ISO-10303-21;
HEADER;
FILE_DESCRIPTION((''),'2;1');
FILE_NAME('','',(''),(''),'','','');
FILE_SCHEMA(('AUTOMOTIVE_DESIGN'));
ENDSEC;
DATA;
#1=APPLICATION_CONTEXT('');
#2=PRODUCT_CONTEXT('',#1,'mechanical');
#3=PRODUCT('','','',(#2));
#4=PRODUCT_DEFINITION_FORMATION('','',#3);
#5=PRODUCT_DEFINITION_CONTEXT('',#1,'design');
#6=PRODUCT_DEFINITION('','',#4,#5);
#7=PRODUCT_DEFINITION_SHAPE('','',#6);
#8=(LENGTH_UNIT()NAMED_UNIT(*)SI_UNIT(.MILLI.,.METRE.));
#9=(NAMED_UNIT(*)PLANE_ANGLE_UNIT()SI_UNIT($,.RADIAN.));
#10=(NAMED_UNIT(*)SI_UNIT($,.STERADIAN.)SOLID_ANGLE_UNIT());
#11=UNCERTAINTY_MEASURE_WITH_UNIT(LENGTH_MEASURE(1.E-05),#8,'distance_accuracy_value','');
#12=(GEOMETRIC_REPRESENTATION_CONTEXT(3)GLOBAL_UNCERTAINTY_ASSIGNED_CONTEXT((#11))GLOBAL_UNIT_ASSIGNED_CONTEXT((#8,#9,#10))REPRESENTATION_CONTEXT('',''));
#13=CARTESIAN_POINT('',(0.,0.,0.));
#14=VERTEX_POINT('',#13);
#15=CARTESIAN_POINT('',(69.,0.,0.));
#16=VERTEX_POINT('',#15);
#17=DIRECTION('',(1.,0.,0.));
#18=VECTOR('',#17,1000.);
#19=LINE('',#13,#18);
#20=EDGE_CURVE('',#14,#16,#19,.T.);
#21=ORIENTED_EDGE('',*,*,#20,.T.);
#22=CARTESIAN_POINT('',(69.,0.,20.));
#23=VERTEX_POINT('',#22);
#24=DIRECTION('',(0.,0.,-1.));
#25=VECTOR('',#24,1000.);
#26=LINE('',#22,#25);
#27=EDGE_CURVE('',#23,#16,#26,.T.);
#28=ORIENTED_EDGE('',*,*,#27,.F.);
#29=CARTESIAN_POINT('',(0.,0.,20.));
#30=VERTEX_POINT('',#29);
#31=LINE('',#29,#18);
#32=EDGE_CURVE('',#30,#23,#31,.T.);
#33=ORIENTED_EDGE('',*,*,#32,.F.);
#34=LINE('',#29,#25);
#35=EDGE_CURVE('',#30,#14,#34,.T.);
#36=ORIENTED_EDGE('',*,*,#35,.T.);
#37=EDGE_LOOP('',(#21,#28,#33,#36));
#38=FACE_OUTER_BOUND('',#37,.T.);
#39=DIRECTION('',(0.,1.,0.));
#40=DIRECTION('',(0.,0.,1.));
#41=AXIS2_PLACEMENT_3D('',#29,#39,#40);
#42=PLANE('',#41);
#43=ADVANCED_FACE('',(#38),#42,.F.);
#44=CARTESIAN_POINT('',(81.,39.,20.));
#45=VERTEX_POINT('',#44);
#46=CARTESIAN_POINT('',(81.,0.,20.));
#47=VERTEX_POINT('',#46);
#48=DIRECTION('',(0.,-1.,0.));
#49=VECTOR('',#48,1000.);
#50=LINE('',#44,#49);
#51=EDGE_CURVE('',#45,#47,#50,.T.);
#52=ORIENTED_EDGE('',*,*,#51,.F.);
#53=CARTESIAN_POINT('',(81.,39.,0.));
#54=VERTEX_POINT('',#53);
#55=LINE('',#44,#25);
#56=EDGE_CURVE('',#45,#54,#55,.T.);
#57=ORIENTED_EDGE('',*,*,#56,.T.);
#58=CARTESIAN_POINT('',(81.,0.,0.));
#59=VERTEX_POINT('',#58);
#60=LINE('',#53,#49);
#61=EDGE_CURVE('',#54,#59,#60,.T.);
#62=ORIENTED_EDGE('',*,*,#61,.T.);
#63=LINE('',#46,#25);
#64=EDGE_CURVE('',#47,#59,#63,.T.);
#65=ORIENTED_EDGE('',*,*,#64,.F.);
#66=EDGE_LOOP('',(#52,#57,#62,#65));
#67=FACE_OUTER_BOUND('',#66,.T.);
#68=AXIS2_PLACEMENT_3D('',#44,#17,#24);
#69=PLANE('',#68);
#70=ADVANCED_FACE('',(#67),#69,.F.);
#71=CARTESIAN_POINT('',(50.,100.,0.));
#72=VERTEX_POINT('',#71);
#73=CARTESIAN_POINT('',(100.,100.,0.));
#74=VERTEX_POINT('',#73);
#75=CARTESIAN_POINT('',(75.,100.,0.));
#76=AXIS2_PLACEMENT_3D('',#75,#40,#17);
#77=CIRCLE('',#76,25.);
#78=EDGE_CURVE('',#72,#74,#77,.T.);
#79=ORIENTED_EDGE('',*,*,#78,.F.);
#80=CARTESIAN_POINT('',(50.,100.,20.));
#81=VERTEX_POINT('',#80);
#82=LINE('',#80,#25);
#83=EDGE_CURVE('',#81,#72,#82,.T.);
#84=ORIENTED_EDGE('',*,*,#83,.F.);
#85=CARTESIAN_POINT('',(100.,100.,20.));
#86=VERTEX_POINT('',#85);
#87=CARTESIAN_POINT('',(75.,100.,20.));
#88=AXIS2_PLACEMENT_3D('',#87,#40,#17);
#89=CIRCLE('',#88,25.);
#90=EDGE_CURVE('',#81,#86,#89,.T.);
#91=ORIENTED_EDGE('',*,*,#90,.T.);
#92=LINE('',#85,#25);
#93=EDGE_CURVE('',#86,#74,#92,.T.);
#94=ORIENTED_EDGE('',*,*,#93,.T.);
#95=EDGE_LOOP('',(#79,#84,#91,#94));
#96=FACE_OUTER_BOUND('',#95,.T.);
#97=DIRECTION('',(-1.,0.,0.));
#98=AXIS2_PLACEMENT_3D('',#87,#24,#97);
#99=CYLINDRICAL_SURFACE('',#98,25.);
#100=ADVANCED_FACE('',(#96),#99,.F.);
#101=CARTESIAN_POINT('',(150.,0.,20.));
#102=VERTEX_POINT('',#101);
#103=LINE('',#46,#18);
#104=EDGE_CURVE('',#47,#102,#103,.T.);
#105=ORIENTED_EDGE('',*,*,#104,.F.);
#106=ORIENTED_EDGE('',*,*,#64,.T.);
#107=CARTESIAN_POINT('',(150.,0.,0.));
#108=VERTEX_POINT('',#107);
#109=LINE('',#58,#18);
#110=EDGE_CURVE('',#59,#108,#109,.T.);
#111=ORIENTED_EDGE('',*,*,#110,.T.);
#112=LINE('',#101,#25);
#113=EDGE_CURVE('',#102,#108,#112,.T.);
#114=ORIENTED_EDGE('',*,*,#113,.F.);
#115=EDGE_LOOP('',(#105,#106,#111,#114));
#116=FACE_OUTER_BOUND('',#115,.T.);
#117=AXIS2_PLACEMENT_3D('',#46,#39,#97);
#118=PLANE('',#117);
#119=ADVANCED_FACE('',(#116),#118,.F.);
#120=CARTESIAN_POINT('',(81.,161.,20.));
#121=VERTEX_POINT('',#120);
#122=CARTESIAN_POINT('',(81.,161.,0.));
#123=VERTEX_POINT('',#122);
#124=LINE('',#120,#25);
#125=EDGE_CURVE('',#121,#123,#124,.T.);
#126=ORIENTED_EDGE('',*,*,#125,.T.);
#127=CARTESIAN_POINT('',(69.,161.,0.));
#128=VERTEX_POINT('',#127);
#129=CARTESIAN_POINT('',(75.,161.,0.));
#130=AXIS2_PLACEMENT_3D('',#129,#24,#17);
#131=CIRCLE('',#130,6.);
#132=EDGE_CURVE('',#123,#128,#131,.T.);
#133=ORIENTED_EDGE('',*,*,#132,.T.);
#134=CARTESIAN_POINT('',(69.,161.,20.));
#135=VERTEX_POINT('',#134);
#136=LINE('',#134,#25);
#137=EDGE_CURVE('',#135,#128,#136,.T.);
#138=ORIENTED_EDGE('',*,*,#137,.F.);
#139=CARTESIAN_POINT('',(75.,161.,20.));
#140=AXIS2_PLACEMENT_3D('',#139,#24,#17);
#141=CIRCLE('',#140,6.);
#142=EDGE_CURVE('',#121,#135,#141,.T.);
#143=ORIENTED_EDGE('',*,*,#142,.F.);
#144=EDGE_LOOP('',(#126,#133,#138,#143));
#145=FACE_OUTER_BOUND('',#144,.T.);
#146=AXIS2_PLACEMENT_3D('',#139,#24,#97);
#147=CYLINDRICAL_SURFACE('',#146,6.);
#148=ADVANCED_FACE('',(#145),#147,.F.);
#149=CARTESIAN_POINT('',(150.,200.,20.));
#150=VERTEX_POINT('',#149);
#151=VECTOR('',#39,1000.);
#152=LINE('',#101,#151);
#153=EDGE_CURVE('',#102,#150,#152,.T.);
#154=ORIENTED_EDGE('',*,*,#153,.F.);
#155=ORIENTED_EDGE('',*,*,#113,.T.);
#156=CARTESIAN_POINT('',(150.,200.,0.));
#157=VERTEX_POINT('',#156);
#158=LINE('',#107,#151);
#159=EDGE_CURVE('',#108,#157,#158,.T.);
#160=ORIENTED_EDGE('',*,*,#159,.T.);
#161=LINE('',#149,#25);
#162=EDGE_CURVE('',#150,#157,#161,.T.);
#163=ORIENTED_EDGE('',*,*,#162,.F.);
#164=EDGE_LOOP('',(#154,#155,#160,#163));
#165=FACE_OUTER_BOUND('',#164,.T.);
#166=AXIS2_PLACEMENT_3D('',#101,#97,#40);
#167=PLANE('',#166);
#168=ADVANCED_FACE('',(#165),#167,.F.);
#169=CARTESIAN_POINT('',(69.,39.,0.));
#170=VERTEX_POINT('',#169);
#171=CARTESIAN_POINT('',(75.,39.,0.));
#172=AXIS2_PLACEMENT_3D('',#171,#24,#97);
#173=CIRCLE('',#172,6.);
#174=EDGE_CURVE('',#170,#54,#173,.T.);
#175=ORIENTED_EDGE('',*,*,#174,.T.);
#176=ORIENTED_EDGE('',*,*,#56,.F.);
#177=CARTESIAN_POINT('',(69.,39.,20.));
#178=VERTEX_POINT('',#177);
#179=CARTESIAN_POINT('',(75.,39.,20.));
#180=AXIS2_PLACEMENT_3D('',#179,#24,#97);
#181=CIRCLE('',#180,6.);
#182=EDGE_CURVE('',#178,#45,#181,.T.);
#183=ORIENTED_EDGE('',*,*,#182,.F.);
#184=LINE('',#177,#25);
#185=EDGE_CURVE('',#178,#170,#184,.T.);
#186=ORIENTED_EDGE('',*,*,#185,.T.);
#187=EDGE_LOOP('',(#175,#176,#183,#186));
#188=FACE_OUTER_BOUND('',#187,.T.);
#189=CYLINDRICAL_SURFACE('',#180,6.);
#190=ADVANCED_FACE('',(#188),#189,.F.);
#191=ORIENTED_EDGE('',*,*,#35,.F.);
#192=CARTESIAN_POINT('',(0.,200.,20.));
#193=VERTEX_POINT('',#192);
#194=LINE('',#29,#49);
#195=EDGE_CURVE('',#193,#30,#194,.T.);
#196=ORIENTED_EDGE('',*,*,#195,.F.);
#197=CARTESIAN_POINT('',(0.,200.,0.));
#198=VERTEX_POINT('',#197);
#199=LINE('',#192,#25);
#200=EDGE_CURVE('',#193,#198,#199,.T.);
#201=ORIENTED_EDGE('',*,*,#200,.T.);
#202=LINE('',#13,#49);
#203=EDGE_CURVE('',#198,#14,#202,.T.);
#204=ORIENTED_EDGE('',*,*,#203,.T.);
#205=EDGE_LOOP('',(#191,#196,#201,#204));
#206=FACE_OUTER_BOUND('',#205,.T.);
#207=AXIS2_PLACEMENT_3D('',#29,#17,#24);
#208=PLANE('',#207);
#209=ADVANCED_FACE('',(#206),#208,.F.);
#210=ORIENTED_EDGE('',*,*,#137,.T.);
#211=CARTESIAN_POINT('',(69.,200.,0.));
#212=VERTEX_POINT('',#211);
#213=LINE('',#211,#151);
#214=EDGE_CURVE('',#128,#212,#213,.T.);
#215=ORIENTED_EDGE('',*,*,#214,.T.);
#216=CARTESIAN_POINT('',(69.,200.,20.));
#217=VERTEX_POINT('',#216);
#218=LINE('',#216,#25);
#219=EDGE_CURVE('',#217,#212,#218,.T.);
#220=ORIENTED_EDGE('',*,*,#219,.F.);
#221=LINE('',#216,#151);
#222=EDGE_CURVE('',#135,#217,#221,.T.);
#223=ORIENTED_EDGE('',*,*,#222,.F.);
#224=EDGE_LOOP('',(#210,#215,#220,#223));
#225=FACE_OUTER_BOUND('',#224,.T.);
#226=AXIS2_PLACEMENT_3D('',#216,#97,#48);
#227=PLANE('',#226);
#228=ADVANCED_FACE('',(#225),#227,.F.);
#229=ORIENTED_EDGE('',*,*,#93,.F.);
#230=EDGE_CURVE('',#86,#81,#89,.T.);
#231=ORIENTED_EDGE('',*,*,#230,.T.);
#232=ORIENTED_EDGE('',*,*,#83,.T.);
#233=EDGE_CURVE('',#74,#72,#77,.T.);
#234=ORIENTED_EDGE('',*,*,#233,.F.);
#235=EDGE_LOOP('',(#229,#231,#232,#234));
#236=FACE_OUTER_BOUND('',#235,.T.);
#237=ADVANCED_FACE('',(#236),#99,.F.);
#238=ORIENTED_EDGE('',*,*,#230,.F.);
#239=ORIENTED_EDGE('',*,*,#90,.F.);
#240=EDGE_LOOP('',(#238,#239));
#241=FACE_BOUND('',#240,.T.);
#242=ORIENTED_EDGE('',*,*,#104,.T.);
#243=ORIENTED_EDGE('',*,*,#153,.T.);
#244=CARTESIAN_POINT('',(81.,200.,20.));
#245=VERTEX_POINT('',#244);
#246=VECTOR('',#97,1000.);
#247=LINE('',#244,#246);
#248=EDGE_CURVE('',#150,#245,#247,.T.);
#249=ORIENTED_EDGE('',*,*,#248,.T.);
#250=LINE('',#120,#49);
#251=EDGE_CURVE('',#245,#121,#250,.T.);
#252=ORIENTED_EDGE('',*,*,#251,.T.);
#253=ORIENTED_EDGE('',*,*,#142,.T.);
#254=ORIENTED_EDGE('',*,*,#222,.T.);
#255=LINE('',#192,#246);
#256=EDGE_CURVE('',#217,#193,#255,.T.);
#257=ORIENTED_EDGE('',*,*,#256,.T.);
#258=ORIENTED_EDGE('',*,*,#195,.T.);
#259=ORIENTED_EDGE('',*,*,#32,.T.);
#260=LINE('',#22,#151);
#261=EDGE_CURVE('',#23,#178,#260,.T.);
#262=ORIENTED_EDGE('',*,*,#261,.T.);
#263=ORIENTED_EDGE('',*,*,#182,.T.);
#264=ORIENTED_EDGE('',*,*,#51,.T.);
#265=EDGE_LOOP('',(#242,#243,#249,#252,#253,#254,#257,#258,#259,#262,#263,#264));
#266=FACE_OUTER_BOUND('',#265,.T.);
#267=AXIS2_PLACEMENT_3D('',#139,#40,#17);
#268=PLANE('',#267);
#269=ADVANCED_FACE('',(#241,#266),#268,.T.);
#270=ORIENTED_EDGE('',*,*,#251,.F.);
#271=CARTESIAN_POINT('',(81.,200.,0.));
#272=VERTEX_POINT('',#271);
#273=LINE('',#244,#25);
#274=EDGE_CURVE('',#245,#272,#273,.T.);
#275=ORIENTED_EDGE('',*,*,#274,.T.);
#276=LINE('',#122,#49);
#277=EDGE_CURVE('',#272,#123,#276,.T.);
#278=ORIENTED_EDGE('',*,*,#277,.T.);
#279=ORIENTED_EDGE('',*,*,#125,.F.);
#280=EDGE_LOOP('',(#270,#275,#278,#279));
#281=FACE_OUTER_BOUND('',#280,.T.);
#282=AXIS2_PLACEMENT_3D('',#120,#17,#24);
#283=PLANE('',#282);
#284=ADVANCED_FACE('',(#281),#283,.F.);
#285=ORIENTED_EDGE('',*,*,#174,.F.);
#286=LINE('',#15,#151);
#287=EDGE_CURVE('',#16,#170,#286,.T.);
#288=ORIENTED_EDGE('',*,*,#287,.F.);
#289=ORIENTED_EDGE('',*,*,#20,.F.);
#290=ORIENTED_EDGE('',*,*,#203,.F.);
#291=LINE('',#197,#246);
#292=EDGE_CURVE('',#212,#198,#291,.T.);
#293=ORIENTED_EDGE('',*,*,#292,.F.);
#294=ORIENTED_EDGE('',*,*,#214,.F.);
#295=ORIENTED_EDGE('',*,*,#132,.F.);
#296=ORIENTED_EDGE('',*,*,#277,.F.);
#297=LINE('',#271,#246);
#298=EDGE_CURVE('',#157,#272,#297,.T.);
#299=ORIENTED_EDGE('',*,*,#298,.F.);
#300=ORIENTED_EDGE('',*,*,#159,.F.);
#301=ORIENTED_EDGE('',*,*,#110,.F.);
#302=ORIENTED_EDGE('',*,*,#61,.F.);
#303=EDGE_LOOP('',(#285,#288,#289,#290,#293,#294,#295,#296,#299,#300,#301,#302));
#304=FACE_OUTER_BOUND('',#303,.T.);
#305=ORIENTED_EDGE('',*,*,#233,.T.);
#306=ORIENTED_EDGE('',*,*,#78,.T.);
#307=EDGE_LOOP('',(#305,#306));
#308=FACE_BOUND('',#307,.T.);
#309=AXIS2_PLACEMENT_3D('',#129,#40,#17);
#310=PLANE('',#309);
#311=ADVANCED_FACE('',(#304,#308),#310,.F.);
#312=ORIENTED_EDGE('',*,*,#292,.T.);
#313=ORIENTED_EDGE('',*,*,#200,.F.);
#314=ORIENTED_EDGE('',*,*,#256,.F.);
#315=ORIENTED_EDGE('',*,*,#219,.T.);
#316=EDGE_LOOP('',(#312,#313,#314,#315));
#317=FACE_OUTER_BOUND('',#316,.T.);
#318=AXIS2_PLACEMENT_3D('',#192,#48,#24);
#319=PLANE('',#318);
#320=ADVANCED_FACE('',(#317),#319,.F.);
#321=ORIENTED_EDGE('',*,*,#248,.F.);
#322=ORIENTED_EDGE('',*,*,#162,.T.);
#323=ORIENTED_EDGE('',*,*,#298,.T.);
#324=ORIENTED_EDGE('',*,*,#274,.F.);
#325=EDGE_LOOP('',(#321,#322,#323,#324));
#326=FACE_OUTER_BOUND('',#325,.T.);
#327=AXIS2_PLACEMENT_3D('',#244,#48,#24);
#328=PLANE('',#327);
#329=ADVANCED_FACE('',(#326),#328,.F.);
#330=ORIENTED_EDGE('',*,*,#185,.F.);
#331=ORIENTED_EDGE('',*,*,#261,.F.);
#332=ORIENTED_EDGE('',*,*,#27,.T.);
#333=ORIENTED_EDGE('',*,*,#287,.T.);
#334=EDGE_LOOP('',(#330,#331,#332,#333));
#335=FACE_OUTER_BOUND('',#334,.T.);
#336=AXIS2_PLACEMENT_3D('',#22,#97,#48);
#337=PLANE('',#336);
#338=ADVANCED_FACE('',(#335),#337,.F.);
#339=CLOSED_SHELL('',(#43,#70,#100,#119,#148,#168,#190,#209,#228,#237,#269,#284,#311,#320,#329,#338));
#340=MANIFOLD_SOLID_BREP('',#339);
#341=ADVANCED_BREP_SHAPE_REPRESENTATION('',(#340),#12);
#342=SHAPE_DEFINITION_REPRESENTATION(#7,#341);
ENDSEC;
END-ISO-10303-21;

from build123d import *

# Parameters (mm, degrees)
SKETCH1_R           = 25
BOSS_EXTRUDE1_DEPTH = 20


with BuildPart() as part:
    # Sketch1 → Boss-Extrude1 (new body)
    with BuildSketch(Plane.XY):
        with BuildLine():
            Line((0, 0), (69, 0))
            Line((69, 0), (69, 39))
            ThreePointArc((69, 39), (75, 45), (81, 39))
            Line((81, 39), (81, 0))
            Line((81, 0), (150, 0))
            Line((150, 0), (150, 200))
            Line((150, 200), (81, 200))
            Line((81, 200), (81, 161))
            ThreePointArc((81, 161), (75, 155), (69, 161))
            Line((69, 161), (69, 200))
            Line((69, 200), (0, 200))
            Line((0, 200), (0, 0))
        make_face()
        with Locations((75, 100)):
            Circle(SKETCH1_R, mode=Mode.SUBTRACT)
    extrude(amount=BOSS_EXTRUDE1_DEPTH)


solid = part.part
